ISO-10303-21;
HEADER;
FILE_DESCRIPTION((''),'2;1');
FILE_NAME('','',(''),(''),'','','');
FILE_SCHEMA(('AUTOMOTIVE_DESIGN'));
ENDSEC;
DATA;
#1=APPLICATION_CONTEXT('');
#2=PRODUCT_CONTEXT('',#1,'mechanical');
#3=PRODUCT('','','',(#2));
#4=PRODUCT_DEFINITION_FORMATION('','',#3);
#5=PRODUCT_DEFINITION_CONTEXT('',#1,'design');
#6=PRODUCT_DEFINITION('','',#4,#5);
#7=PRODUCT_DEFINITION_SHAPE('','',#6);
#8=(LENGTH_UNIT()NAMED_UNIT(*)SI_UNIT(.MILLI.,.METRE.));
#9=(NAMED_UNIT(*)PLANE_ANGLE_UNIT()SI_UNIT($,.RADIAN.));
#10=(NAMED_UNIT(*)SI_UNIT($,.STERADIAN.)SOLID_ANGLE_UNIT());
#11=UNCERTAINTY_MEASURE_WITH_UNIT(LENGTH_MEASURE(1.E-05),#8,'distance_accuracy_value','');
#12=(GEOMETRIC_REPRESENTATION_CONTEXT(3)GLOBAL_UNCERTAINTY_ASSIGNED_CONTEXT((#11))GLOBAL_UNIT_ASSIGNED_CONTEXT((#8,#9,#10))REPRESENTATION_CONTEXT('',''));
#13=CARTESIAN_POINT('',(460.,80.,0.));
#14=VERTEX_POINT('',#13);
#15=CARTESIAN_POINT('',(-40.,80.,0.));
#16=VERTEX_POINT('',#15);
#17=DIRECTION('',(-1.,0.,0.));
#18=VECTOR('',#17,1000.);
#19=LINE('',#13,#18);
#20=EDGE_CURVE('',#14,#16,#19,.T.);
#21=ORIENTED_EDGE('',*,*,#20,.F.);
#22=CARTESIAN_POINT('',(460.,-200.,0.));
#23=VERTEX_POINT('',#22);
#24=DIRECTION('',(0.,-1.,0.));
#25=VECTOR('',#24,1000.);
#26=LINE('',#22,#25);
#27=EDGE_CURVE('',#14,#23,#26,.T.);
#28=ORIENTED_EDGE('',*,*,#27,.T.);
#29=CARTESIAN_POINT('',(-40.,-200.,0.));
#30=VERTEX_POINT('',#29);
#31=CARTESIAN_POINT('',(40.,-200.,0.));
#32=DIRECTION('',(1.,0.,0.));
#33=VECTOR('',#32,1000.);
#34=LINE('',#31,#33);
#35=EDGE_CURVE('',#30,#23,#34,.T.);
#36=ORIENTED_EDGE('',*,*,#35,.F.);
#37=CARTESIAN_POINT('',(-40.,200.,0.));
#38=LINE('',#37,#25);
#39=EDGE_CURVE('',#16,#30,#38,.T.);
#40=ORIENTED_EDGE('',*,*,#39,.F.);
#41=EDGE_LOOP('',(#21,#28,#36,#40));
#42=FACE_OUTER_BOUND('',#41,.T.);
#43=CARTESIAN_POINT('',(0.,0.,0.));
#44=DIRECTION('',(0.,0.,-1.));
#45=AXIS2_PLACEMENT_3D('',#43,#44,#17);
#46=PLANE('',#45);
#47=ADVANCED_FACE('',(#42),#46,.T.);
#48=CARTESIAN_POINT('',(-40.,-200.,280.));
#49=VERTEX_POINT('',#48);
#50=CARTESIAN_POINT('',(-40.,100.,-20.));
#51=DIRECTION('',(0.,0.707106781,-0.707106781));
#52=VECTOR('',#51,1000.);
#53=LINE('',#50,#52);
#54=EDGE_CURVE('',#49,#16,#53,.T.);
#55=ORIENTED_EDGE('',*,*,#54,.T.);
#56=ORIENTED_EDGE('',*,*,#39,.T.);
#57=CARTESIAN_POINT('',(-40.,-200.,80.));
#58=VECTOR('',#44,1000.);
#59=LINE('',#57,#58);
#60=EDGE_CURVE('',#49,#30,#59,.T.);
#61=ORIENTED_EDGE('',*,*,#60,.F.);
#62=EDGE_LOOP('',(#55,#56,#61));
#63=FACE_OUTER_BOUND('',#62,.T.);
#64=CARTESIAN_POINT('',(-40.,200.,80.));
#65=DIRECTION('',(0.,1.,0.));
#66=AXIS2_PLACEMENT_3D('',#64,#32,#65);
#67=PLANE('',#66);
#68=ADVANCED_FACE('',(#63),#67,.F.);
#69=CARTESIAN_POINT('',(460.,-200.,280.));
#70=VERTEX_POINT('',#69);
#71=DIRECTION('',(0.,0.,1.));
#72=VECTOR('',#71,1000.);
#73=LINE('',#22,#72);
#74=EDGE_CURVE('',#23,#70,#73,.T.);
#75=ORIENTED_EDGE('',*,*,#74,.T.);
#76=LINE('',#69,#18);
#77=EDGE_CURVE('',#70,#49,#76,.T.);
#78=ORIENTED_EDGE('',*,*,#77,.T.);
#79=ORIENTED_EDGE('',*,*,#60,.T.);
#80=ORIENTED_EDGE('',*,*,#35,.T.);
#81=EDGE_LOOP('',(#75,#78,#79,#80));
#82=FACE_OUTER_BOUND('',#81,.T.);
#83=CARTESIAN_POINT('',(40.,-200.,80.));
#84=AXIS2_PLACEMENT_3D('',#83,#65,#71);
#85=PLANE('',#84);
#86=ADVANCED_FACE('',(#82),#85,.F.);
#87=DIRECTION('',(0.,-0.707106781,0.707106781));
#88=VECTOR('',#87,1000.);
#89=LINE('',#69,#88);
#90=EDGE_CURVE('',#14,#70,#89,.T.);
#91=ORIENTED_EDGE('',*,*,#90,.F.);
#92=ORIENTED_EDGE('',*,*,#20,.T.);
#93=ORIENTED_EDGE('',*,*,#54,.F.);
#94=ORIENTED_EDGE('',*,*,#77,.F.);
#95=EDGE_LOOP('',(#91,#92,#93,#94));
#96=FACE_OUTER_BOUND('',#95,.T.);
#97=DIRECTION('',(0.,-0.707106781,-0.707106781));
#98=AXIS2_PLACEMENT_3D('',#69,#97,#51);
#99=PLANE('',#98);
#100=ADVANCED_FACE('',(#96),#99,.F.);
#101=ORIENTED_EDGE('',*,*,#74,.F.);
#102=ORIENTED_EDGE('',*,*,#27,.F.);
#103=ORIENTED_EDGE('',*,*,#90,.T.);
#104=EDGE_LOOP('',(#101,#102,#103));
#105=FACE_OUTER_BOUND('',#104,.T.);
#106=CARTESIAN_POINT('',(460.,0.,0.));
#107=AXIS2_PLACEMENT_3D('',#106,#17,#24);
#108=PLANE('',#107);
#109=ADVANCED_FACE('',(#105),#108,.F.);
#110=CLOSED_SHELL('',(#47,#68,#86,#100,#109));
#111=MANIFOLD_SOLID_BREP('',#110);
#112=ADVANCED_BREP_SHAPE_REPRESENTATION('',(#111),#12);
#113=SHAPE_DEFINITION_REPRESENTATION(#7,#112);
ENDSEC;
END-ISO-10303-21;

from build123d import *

# Parameters (mm, degrees)
SKETCH1_W               = 80
SKETCH1_H               = 400
BOSS_EXTRUDE1_DEPTH     = 80
BOSS_EXTRUDE2_DEPTH     = 80
CUT_EXTRUDE1_DEPTH      = 300
BOSS_EXTRUDE3_DEPTH     = 500
CUT_EXTRUDE2_DEPTH      = 718.63500472
CUT_EXTRUDE2_DEPTH_BACK = 718.63500472


with BuildPart() as part:
    # Sketch1 → Boss-Extrude1 (new body)
    with BuildSketch(Plane.XY):
        Rectangle(SKETCH1_W, SKETCH1_H)
    extrude(amount=BOSS_EXTRUDE1_DEPTH)

    # Sketch2 → Boss-Extrude2 (add)
    with BuildSketch(Plane.ZY.offset(40)):
        Polygon((0, -200), (400, -200), (0, 200), align=None)
    extrude(amount=-BOSS_EXTRUDE2_DEPTH)

    # Sketch3 → Cut-Extrude1 (cut)
    with BuildSketch(Plane.ZY.offset(40)):
        Polygon((80, 120), (0, 200), (172.987961084, 200), align=None)
    extrude(amount=-CUT_EXTRUDE1_DEPTH, mode=Mode.SUBTRACT)

    # Sketch4 → Boss-Extrude3 (add)
    with BuildSketch(Plane.ZY.offset(40)):
        Polygon((0, -200), (0, 250), (450, -200), align=None)
    extrude(amount=-BOSS_EXTRUDE3_DEPTH)

    # Sketch5 → Cut-Extrude2 (cut, two sides: drawn at the far end of the back side and taken through both)
    with BuildSketch(Plane.ZY.offset(40).offset(-CUT_EXTRUDE2_DEPTH_BACK)):
        Polygon((280, -200), (0, 80), (0, 250), (450, -200), align=None)
    extrude(amount=CUT_EXTRUDE2_DEPTH + CUT_EXTRUDE2_DEPTH_BACK, mode=Mode.SUBTRACT)


solid = part.part
